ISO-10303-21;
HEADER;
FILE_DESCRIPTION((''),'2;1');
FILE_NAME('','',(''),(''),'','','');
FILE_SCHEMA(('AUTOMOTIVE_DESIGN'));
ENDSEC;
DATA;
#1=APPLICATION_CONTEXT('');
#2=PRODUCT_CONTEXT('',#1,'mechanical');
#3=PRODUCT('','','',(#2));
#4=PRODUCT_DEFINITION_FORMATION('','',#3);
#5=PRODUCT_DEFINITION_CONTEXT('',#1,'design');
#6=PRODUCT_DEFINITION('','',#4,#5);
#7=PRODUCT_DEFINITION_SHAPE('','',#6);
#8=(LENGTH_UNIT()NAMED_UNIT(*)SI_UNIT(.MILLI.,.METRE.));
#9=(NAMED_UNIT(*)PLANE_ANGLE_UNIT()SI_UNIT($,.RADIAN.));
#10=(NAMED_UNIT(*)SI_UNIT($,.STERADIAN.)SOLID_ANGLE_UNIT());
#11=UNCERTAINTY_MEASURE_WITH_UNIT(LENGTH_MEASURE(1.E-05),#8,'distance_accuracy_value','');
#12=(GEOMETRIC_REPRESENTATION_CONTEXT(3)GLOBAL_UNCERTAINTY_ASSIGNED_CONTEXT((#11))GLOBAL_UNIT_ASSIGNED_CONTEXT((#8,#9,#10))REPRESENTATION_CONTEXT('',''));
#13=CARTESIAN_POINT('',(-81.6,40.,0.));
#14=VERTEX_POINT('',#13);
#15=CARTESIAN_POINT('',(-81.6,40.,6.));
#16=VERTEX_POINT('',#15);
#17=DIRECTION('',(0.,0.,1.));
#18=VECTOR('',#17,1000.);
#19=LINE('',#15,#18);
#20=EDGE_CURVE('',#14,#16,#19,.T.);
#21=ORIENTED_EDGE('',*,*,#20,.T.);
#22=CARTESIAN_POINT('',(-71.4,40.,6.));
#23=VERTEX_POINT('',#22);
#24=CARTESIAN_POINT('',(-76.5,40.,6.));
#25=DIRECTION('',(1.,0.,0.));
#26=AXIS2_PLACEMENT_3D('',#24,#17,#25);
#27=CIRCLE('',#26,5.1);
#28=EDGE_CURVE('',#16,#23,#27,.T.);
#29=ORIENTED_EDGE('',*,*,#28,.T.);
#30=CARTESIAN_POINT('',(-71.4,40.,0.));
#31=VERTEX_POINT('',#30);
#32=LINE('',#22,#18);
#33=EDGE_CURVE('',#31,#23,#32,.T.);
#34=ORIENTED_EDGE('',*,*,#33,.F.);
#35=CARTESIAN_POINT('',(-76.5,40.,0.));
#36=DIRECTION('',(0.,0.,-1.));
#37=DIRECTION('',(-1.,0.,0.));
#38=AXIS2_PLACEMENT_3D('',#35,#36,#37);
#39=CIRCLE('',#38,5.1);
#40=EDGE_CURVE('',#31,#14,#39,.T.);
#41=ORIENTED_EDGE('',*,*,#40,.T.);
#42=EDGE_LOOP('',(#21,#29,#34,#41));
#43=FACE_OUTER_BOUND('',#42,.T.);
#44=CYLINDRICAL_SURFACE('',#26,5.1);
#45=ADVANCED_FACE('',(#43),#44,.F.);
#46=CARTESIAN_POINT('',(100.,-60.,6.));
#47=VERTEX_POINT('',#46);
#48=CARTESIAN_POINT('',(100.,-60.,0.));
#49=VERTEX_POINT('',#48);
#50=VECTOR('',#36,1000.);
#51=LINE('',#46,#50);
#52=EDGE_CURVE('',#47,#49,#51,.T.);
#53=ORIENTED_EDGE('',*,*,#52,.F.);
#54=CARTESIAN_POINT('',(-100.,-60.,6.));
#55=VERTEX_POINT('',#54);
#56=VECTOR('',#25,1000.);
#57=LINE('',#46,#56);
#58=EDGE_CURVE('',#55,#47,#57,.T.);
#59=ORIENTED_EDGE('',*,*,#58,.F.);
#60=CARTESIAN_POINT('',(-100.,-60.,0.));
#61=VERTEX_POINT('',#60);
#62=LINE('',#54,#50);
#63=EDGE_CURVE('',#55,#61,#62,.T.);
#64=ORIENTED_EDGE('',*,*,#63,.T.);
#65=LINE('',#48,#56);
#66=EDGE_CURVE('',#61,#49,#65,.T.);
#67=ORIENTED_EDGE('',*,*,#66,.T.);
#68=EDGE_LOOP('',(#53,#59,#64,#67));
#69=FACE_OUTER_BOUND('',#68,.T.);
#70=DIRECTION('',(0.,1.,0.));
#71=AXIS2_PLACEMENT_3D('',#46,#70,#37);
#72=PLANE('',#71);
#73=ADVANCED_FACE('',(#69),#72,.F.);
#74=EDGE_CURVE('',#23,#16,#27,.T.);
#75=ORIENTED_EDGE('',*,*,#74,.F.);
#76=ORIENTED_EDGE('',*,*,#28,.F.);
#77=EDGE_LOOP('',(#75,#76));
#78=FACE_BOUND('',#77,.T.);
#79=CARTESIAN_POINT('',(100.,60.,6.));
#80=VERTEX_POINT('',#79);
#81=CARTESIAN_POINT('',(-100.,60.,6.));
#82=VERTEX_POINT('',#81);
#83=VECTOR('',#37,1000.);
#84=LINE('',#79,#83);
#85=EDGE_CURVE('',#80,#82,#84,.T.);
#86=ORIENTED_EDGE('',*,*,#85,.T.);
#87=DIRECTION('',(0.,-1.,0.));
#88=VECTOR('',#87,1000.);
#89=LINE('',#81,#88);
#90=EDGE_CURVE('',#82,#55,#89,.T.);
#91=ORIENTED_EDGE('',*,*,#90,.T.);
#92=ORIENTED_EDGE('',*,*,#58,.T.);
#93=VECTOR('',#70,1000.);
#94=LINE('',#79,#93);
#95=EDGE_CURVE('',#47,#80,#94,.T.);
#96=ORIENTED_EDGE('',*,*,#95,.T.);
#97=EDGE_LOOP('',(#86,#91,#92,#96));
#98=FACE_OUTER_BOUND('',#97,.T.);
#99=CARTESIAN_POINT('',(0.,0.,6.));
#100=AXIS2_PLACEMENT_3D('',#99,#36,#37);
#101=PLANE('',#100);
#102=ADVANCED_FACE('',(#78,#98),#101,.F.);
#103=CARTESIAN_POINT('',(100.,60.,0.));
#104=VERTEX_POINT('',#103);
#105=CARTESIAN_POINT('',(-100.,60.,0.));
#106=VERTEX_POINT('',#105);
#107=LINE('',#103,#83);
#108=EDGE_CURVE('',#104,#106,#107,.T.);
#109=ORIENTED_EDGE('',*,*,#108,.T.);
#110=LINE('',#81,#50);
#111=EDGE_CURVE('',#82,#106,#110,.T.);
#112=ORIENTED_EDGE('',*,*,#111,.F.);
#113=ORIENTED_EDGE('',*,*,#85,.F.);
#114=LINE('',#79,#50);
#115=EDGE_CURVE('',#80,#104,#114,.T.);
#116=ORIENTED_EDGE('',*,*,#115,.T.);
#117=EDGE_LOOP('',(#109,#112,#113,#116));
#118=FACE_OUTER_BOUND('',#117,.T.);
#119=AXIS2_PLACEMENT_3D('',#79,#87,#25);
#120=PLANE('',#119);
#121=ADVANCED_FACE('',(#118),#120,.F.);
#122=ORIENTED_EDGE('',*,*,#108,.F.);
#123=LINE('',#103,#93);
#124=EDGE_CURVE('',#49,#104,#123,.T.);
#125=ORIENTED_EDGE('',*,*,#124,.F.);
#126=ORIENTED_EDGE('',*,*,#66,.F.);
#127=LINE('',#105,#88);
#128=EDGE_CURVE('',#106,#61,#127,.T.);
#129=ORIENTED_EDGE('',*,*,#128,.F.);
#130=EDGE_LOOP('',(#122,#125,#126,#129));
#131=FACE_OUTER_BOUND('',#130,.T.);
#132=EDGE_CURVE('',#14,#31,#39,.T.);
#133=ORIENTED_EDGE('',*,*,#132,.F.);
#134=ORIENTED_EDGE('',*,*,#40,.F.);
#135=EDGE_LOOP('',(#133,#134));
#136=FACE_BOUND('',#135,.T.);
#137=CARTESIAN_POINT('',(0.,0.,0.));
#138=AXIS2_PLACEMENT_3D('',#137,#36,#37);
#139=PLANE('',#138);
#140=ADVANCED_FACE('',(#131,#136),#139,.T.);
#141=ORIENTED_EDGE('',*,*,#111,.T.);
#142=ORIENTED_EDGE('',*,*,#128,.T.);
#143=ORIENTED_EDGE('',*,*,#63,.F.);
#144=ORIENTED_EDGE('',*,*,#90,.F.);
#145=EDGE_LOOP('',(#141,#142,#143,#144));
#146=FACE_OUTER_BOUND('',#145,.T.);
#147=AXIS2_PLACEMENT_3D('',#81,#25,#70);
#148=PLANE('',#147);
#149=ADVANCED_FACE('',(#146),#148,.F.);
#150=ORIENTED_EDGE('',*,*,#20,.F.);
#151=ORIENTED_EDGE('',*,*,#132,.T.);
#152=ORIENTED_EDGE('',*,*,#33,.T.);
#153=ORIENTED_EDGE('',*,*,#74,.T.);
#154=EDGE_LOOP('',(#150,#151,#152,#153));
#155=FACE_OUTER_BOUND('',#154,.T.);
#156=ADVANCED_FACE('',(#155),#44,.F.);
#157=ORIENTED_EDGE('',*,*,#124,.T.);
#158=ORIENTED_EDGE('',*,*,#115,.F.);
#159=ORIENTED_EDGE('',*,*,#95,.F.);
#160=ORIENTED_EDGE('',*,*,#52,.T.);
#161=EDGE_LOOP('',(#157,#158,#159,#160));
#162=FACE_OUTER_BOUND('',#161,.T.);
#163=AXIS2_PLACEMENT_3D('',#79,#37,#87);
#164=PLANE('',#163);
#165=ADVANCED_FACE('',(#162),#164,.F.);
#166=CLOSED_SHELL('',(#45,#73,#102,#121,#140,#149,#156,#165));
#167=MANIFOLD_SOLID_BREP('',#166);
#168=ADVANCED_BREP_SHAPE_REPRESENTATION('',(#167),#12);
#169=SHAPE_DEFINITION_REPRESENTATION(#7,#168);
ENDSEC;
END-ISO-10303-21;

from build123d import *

# Parameters (mm, degrees)
SKETCH1_W              = 200
SKETCH1_H              = 120
BOSS_EXTRUDE1_DEPTH    = 6
M12_TAPPED_HOLE1_D     = 10.2
M12_TAPPED_HOLE1_DEPTH = 29.25
M12_TAPPED_HOLE1_TIP   = 3.064389157


with BuildPart() as part:
    # Sketch1 → Boss-Extrude1 (new body)
    with BuildSketch(Plane.XY):
        Rectangle(SKETCH1_W, SKETCH1_H)
    extrude(amount=BOSS_EXTRUDE1_DEPTH)

    # M12 Tapped Hole1
    with Locations(Plane.XY.offset(6)):
        with Locations((-76.5, 40)):
            Hole(M12_TAPPED_HOLE1_D / 2, depth=M12_TAPPED_HOLE1_DEPTH)
            with Locations((0, 0, -(M12_TAPPED_HOLE1_DEPTH + M12_TAPPED_HOLE1_TIP / 2))):  # 118° drill point
                Cone(0, M12_TAPPED_HOLE1_D / 2, M12_TAPPED_HOLE1_TIP, mode=Mode.SUBTRACT)


solid = part.part
